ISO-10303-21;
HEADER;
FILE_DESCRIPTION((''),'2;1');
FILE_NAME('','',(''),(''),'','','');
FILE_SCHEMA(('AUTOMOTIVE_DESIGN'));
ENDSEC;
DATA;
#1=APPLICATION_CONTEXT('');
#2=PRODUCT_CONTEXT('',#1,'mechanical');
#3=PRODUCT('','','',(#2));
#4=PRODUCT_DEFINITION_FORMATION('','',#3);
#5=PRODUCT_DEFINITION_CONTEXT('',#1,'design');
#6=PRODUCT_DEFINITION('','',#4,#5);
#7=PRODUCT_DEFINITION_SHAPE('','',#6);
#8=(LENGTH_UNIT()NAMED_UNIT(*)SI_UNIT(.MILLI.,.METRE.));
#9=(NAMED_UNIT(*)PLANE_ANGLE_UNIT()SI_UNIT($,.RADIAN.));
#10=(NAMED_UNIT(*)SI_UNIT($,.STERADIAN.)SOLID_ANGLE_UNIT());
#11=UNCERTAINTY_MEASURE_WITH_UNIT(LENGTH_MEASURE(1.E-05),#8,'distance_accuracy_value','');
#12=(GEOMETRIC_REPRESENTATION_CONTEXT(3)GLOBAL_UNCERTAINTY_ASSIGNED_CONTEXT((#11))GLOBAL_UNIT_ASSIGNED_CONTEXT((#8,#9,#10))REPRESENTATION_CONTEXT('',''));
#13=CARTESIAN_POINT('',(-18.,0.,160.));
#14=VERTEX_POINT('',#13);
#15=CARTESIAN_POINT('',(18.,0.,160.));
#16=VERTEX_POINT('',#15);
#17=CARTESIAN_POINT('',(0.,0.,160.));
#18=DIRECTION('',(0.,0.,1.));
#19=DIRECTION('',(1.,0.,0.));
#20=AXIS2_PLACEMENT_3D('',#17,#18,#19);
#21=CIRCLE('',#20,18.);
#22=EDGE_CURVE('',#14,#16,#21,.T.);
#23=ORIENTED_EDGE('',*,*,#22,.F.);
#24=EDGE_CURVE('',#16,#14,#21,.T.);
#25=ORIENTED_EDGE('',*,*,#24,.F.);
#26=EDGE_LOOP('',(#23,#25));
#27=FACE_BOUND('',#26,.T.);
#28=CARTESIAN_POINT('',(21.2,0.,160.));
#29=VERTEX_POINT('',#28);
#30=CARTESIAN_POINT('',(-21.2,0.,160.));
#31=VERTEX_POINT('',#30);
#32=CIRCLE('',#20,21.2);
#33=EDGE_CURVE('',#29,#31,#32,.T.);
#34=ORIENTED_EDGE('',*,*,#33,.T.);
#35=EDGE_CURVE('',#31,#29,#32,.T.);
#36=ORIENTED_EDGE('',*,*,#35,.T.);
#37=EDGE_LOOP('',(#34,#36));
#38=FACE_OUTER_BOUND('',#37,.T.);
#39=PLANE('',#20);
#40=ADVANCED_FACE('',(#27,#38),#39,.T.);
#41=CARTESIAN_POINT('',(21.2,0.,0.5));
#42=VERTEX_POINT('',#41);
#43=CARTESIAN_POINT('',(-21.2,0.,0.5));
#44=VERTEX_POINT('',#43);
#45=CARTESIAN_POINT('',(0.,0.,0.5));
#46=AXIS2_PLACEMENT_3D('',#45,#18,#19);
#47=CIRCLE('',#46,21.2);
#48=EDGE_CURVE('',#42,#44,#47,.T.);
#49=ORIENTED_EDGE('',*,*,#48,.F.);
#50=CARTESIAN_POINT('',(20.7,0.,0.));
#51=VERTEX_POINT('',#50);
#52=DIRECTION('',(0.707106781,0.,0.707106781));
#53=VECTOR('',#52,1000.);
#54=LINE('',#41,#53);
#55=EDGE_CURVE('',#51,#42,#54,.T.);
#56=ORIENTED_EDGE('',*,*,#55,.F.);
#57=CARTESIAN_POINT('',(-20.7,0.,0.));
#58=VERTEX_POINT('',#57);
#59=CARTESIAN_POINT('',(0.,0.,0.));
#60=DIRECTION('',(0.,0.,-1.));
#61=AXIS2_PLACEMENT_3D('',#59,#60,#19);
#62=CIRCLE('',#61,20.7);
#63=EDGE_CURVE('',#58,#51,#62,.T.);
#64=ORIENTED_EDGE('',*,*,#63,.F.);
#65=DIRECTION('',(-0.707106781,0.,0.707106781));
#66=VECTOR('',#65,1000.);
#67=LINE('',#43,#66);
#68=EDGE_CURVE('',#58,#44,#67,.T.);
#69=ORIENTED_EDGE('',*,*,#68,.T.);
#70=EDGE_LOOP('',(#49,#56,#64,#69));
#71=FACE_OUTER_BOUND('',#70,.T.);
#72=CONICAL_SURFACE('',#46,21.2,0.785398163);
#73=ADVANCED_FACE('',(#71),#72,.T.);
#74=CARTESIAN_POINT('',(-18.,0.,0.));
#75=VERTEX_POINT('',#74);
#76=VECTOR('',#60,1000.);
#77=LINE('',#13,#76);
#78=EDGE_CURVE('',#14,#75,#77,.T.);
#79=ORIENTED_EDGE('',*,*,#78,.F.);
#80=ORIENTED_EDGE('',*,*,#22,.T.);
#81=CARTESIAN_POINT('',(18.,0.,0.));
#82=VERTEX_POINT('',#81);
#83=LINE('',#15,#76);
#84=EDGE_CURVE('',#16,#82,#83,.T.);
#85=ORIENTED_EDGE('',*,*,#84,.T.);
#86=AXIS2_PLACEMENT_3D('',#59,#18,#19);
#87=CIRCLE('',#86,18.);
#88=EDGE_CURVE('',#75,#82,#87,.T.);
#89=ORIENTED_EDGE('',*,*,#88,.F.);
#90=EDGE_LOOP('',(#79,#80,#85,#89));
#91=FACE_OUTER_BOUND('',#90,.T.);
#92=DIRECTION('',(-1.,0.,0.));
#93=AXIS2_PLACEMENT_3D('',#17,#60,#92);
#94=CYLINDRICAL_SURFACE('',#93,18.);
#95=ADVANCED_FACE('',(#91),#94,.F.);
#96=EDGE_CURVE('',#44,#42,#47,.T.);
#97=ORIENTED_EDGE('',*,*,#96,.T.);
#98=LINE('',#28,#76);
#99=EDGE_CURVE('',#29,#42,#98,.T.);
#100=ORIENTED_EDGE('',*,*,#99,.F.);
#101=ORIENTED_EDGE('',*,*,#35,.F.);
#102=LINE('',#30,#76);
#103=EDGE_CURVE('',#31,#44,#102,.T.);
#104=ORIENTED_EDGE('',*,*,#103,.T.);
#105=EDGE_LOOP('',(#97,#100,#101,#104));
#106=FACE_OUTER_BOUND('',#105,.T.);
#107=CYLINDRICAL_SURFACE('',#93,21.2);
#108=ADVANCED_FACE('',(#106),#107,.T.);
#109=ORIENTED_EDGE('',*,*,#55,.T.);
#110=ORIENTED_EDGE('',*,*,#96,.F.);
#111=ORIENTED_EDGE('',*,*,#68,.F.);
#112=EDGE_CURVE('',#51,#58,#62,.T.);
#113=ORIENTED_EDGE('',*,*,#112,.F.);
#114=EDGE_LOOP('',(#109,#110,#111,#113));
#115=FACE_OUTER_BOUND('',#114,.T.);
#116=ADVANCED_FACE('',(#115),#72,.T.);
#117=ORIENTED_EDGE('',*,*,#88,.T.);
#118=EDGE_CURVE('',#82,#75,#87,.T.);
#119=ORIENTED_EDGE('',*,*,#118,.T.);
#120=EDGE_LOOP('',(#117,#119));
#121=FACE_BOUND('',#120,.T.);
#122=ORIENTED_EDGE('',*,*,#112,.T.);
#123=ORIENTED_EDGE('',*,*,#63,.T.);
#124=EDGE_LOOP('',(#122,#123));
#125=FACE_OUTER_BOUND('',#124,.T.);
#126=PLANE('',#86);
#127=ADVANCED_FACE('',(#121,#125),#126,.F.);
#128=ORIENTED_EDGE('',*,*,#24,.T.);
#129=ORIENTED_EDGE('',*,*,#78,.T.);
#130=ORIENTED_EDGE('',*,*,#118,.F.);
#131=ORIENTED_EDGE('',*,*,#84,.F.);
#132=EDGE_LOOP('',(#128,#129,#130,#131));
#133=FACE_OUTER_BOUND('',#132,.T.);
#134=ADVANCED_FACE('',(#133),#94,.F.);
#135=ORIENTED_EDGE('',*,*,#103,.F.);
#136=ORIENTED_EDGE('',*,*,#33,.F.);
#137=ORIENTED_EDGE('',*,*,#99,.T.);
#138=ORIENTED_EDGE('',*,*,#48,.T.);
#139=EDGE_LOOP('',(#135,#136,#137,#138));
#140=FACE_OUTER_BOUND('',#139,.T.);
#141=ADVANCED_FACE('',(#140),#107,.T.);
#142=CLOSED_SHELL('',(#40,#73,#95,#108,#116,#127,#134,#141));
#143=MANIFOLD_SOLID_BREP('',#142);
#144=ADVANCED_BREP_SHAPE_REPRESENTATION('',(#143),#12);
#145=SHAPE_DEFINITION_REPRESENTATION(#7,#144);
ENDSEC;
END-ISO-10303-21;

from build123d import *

# Parameters (mm, degrees)
SKETCH_1_R      = 21.2
EXTRUDE_1_DEPTH = 160
SHELL_1_T       = -3.2
CHAMFER_1_SIZE  = 0.5


with BuildPart() as part:
    # 草图1 → 凸台-拉伸1 (new body)
    with BuildSketch(Plane.XY):
        Circle(SKETCH_1_R)
    extrude(amount=EXTRUDE_1_DEPTH)

    # 抽壳1
    shell_1_openings = [part.faces().sort_by_distance(p)[0] for p in [
        (0, 0, 160),
        (0, 0, 0),
    ]]
    offset(amount=SHELL_1_T, openings=shell_1_openings, kind=Kind.INTERSECTION)

    # 倒角1
    chamfer_1_edges = [part.edges().sort_by_distance(p)[0] for p in [
        (-21.2, 0, 0),
    ]]
    chamfer(chamfer_1_edges, length=CHAMFER_1_SIZE)


solid = part.part
